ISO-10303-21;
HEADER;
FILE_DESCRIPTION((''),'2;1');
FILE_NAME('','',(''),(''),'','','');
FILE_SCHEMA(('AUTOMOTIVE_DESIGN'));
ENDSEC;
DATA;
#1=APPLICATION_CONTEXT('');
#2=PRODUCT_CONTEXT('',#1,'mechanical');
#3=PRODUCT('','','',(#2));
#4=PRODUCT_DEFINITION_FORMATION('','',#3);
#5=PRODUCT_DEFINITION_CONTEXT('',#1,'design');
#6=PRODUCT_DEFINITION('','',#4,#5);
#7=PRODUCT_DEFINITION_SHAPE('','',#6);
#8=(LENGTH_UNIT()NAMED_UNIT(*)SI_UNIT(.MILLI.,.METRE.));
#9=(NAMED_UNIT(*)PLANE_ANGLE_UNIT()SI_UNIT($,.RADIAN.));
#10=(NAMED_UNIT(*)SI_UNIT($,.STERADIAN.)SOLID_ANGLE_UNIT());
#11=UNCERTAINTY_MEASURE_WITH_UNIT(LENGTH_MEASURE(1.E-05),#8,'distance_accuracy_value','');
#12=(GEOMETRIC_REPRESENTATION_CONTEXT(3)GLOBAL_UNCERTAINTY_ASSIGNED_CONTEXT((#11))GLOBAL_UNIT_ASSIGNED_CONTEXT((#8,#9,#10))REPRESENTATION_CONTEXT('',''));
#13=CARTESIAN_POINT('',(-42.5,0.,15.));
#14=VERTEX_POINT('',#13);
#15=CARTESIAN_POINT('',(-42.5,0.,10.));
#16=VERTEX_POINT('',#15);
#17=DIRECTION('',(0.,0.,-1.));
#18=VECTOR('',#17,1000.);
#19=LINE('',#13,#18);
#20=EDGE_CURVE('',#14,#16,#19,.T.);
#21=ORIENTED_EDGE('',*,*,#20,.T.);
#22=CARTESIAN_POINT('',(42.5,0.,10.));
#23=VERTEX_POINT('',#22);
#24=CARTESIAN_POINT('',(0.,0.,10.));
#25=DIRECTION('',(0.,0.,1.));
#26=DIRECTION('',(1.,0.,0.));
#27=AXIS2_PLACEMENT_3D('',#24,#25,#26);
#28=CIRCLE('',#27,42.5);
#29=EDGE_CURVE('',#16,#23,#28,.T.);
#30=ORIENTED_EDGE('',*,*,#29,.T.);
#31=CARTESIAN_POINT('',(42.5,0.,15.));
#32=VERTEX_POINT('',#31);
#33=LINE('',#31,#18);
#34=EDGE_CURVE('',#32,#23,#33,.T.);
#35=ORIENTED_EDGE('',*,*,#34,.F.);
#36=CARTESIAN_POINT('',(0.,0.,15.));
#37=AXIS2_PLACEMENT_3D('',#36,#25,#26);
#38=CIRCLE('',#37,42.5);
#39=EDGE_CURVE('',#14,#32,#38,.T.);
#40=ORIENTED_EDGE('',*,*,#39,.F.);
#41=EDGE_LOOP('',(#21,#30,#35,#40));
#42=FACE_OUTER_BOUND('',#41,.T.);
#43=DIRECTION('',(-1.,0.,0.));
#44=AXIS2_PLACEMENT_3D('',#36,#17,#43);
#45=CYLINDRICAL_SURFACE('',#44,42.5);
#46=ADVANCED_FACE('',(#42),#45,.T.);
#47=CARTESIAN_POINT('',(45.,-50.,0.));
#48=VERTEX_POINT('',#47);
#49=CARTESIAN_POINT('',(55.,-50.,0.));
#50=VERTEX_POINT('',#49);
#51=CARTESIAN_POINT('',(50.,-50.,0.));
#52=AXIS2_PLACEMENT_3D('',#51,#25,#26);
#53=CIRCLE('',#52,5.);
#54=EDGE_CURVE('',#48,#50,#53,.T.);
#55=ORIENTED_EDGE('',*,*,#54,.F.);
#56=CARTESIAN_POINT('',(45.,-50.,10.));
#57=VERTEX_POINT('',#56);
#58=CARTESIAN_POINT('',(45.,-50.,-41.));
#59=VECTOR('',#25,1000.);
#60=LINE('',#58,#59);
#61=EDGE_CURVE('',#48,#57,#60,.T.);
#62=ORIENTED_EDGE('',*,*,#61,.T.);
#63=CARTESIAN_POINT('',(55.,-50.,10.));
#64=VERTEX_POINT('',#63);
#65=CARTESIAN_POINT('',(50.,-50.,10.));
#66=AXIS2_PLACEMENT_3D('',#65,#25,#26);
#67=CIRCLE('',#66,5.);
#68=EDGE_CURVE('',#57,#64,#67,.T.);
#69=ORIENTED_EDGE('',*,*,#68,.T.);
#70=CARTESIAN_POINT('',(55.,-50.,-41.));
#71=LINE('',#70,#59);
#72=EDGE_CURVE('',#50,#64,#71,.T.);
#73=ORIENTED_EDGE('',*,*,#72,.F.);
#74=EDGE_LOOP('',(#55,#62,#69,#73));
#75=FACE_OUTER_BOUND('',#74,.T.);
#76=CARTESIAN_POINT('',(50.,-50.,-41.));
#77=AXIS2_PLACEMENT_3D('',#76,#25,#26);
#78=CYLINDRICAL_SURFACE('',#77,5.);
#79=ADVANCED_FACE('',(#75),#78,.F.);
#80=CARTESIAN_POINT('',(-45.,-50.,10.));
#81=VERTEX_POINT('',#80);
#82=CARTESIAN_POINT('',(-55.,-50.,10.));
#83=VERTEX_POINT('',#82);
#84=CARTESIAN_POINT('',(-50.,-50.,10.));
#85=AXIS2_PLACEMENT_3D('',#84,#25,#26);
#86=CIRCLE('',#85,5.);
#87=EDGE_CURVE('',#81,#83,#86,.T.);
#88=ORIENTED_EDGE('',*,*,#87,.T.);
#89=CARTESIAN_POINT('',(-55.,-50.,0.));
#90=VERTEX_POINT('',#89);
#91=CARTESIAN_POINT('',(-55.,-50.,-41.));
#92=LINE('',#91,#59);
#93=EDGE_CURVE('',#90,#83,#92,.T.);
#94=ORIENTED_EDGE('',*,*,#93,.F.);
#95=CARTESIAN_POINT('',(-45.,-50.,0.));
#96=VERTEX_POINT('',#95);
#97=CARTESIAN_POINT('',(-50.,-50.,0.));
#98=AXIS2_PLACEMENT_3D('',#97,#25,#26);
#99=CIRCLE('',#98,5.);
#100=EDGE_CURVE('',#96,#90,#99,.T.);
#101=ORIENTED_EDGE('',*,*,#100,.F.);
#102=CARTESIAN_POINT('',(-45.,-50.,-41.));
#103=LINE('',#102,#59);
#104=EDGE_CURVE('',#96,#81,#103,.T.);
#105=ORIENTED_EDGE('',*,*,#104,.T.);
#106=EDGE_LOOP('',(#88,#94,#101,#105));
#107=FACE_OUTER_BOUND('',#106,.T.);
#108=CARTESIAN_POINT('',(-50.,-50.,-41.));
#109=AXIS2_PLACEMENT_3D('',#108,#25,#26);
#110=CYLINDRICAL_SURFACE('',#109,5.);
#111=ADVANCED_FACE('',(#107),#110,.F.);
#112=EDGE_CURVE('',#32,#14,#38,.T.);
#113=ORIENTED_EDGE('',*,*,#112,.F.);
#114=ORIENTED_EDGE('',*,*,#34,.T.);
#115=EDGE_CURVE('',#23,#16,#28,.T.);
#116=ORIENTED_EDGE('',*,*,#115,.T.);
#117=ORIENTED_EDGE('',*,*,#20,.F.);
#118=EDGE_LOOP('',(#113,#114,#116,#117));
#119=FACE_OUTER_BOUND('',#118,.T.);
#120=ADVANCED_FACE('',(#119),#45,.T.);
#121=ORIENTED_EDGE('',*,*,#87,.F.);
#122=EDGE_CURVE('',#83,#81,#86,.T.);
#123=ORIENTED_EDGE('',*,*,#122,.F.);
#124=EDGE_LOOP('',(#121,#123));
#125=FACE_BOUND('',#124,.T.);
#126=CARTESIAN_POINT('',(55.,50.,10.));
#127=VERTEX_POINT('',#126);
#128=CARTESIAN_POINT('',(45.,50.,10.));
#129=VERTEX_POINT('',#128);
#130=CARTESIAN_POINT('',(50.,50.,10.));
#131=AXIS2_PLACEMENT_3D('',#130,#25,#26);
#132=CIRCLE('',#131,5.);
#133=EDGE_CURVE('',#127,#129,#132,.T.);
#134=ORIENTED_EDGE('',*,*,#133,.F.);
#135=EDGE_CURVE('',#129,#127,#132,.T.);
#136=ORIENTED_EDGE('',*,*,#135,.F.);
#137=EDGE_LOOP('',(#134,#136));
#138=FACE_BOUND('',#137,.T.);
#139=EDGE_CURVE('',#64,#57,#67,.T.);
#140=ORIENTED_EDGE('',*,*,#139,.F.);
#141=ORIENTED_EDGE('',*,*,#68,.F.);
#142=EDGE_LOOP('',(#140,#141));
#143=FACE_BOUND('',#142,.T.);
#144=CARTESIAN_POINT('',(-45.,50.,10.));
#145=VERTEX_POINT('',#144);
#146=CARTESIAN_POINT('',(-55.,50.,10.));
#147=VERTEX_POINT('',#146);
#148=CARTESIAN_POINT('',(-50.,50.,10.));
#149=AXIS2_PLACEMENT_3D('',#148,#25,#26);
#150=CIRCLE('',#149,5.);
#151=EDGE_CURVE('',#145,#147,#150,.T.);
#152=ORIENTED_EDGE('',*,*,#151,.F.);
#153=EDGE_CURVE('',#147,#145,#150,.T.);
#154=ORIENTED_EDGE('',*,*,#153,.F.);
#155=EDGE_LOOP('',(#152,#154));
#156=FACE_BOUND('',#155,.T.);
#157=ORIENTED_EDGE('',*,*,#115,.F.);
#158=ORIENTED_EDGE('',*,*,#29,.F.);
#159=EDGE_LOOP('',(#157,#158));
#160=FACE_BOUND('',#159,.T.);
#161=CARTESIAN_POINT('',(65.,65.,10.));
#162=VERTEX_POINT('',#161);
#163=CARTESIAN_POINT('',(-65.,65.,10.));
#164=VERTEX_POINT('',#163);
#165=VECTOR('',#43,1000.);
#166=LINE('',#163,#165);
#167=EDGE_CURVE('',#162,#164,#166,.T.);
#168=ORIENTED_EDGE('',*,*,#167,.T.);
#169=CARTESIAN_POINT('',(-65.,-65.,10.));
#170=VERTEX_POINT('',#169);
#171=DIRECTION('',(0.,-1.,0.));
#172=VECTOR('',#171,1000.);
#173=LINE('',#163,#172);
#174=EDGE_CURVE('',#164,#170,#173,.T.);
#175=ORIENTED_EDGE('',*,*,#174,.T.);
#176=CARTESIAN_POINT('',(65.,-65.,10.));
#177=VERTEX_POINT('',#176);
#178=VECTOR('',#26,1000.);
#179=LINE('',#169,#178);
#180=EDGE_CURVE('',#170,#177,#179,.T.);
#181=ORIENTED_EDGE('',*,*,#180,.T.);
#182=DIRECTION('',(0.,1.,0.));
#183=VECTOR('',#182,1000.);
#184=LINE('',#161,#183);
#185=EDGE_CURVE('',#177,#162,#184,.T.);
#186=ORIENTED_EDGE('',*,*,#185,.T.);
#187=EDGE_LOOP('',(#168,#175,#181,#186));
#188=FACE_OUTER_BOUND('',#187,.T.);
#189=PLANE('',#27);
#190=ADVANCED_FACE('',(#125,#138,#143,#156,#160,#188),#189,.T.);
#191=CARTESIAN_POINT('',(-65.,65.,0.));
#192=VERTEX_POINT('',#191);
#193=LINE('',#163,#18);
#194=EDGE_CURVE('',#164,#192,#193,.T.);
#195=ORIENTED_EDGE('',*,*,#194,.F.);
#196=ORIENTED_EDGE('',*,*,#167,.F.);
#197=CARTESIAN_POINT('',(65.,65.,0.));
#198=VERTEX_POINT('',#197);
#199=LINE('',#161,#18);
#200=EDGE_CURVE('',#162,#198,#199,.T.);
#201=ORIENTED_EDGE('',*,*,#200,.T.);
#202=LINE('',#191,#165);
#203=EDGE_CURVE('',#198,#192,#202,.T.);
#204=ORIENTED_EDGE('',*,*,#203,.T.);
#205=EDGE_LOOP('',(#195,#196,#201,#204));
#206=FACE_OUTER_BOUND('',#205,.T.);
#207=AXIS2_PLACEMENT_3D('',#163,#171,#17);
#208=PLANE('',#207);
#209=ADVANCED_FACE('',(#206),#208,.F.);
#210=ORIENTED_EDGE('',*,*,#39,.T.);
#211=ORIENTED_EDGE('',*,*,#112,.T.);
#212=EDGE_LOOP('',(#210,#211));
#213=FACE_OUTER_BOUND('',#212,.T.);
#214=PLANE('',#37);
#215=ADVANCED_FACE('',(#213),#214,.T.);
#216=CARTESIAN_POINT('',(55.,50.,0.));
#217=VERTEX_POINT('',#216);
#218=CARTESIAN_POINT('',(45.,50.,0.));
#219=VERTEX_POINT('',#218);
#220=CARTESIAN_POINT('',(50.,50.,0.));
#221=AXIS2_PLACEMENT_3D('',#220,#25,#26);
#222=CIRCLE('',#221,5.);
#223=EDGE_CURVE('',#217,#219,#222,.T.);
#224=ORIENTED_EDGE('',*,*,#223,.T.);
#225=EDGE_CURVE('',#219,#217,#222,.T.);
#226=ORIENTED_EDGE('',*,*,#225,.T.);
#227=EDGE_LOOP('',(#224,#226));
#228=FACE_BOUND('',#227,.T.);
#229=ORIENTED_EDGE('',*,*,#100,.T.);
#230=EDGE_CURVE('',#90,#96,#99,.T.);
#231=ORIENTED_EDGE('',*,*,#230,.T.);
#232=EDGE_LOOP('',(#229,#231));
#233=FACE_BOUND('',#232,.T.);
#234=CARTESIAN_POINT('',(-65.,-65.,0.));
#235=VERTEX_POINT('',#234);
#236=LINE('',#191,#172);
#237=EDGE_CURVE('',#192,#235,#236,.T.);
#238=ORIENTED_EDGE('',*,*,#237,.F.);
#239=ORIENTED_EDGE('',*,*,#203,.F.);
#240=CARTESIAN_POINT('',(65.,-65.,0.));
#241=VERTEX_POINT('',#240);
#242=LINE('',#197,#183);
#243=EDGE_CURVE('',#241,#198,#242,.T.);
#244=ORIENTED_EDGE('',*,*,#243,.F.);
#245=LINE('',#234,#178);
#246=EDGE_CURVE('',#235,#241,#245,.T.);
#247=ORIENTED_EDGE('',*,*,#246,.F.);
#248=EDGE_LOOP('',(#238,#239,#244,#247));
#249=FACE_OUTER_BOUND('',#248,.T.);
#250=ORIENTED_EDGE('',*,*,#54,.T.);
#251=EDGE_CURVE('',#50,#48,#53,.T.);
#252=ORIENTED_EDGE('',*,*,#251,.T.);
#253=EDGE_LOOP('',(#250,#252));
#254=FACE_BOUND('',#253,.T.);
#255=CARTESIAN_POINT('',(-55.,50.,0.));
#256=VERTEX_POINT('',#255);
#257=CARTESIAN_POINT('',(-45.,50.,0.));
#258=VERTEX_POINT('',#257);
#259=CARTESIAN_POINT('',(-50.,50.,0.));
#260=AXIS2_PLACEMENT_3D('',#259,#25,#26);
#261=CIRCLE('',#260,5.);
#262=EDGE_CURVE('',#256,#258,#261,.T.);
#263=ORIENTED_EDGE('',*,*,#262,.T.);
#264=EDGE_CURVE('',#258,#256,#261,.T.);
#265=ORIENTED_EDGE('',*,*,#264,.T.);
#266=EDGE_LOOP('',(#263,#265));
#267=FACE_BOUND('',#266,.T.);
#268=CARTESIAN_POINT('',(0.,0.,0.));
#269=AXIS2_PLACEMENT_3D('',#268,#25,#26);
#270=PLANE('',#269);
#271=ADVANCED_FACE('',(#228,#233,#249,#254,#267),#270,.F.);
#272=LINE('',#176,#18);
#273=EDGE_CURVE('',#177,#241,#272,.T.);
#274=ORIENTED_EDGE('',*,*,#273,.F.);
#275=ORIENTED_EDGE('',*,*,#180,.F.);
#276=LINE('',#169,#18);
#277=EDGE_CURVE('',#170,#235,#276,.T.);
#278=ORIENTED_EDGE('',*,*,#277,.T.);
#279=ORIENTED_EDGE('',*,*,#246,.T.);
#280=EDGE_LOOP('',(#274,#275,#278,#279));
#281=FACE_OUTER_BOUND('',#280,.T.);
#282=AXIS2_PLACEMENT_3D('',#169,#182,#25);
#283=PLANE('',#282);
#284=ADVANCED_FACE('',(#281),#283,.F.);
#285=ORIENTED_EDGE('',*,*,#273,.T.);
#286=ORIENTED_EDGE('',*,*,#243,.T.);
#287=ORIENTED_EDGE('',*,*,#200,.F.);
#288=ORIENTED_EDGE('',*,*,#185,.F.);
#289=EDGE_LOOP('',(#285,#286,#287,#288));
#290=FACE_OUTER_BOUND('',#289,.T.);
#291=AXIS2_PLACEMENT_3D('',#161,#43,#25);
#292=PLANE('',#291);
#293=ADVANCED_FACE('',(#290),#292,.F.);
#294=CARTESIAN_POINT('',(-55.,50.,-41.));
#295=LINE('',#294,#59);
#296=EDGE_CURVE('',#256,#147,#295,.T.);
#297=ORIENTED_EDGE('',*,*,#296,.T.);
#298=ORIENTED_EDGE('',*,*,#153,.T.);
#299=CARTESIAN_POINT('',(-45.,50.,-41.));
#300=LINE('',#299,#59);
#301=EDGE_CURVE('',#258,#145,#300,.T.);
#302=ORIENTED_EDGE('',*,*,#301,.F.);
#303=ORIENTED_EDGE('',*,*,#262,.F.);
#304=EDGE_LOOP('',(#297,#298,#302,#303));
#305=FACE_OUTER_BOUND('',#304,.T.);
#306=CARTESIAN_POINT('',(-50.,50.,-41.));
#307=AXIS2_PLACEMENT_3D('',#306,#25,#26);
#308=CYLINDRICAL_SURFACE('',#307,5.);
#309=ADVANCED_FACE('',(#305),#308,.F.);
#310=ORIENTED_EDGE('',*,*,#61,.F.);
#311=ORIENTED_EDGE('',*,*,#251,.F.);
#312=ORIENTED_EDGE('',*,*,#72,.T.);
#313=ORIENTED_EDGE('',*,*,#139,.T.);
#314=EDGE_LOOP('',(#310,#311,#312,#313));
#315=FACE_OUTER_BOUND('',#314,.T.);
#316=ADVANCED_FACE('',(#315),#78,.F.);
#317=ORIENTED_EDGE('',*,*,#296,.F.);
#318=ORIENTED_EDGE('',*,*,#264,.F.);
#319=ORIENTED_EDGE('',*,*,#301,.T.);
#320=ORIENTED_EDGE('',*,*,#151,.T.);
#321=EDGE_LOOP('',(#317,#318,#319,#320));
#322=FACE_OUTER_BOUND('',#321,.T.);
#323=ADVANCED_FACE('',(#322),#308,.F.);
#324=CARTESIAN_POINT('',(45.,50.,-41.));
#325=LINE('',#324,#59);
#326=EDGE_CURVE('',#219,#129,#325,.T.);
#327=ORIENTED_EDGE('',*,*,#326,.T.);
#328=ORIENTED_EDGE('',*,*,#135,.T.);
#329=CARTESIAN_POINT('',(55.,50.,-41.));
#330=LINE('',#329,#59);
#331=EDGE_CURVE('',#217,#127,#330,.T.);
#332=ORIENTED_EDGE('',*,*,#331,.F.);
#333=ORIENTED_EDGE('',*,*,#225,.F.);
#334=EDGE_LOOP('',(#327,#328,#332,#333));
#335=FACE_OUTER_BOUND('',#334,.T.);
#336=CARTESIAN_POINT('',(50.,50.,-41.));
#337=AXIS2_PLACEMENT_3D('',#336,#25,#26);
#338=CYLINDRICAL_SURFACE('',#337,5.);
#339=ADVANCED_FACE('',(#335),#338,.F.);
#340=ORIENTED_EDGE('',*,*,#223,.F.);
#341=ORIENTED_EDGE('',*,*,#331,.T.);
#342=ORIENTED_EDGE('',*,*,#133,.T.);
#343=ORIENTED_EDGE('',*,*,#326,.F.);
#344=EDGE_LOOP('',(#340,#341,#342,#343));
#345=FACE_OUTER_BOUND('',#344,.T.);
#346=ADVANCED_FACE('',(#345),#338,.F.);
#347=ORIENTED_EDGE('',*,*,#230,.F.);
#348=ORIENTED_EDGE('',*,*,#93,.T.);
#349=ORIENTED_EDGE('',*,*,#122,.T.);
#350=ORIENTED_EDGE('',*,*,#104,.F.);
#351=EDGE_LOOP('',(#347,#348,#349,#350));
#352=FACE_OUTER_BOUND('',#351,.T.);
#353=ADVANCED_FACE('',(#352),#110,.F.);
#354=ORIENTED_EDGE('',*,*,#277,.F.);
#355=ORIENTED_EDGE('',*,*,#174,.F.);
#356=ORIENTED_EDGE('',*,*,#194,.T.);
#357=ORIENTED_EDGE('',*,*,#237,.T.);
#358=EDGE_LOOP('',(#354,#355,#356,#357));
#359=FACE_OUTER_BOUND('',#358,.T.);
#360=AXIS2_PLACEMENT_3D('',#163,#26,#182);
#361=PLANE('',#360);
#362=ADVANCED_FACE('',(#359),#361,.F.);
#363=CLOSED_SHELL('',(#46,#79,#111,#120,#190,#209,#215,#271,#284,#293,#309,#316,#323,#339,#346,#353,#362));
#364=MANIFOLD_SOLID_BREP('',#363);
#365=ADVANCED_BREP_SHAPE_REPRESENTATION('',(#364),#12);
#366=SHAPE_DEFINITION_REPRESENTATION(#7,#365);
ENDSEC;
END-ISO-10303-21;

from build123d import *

# Parameters (mm, degrees)
SKETCH1_W           = 130
SKETCH1_H           = 130
BOSS_EXTRUDE1_DEPTH = 10
SKETCH2_R           = 42.5
BOSS_EXTRUDE2_DEPTH = 5
SKETCH3_R           = 5
CUT_EXTRUDE1_DEPTH  = 51


with BuildPart() as part:
    # Sketch1 → Boss-Extrude1 (new body)
    with BuildSketch(Plane.XY):
        Rectangle(SKETCH1_W, SKETCH1_H)
    extrude(amount=BOSS_EXTRUDE1_DEPTH)

    # Sketch2 → Boss-Extrude2 (add)
    with BuildSketch(Plane.XY.offset(10)):
        Circle(SKETCH2_R)
    extrude(amount=BOSS_EXTRUDE2_DEPTH)

    # Sketch3 → Cut-Extrude1 (cut)
    with BuildSketch(Plane.XY.offset(10)):
        with Locations((50, 50)):
            Circle(SKETCH3_R)
        with Locations((-50, 50)):
            Circle(SKETCH3_R)
        with Locations((-50, -50)):
            Circle(SKETCH3_R)
        with Locations((50, -50)):
            Circle(SKETCH3_R)
    extrude(amount=-CUT_EXTRUDE1_DEPTH, mode=Mode.SUBTRACT)


solid = part.part
